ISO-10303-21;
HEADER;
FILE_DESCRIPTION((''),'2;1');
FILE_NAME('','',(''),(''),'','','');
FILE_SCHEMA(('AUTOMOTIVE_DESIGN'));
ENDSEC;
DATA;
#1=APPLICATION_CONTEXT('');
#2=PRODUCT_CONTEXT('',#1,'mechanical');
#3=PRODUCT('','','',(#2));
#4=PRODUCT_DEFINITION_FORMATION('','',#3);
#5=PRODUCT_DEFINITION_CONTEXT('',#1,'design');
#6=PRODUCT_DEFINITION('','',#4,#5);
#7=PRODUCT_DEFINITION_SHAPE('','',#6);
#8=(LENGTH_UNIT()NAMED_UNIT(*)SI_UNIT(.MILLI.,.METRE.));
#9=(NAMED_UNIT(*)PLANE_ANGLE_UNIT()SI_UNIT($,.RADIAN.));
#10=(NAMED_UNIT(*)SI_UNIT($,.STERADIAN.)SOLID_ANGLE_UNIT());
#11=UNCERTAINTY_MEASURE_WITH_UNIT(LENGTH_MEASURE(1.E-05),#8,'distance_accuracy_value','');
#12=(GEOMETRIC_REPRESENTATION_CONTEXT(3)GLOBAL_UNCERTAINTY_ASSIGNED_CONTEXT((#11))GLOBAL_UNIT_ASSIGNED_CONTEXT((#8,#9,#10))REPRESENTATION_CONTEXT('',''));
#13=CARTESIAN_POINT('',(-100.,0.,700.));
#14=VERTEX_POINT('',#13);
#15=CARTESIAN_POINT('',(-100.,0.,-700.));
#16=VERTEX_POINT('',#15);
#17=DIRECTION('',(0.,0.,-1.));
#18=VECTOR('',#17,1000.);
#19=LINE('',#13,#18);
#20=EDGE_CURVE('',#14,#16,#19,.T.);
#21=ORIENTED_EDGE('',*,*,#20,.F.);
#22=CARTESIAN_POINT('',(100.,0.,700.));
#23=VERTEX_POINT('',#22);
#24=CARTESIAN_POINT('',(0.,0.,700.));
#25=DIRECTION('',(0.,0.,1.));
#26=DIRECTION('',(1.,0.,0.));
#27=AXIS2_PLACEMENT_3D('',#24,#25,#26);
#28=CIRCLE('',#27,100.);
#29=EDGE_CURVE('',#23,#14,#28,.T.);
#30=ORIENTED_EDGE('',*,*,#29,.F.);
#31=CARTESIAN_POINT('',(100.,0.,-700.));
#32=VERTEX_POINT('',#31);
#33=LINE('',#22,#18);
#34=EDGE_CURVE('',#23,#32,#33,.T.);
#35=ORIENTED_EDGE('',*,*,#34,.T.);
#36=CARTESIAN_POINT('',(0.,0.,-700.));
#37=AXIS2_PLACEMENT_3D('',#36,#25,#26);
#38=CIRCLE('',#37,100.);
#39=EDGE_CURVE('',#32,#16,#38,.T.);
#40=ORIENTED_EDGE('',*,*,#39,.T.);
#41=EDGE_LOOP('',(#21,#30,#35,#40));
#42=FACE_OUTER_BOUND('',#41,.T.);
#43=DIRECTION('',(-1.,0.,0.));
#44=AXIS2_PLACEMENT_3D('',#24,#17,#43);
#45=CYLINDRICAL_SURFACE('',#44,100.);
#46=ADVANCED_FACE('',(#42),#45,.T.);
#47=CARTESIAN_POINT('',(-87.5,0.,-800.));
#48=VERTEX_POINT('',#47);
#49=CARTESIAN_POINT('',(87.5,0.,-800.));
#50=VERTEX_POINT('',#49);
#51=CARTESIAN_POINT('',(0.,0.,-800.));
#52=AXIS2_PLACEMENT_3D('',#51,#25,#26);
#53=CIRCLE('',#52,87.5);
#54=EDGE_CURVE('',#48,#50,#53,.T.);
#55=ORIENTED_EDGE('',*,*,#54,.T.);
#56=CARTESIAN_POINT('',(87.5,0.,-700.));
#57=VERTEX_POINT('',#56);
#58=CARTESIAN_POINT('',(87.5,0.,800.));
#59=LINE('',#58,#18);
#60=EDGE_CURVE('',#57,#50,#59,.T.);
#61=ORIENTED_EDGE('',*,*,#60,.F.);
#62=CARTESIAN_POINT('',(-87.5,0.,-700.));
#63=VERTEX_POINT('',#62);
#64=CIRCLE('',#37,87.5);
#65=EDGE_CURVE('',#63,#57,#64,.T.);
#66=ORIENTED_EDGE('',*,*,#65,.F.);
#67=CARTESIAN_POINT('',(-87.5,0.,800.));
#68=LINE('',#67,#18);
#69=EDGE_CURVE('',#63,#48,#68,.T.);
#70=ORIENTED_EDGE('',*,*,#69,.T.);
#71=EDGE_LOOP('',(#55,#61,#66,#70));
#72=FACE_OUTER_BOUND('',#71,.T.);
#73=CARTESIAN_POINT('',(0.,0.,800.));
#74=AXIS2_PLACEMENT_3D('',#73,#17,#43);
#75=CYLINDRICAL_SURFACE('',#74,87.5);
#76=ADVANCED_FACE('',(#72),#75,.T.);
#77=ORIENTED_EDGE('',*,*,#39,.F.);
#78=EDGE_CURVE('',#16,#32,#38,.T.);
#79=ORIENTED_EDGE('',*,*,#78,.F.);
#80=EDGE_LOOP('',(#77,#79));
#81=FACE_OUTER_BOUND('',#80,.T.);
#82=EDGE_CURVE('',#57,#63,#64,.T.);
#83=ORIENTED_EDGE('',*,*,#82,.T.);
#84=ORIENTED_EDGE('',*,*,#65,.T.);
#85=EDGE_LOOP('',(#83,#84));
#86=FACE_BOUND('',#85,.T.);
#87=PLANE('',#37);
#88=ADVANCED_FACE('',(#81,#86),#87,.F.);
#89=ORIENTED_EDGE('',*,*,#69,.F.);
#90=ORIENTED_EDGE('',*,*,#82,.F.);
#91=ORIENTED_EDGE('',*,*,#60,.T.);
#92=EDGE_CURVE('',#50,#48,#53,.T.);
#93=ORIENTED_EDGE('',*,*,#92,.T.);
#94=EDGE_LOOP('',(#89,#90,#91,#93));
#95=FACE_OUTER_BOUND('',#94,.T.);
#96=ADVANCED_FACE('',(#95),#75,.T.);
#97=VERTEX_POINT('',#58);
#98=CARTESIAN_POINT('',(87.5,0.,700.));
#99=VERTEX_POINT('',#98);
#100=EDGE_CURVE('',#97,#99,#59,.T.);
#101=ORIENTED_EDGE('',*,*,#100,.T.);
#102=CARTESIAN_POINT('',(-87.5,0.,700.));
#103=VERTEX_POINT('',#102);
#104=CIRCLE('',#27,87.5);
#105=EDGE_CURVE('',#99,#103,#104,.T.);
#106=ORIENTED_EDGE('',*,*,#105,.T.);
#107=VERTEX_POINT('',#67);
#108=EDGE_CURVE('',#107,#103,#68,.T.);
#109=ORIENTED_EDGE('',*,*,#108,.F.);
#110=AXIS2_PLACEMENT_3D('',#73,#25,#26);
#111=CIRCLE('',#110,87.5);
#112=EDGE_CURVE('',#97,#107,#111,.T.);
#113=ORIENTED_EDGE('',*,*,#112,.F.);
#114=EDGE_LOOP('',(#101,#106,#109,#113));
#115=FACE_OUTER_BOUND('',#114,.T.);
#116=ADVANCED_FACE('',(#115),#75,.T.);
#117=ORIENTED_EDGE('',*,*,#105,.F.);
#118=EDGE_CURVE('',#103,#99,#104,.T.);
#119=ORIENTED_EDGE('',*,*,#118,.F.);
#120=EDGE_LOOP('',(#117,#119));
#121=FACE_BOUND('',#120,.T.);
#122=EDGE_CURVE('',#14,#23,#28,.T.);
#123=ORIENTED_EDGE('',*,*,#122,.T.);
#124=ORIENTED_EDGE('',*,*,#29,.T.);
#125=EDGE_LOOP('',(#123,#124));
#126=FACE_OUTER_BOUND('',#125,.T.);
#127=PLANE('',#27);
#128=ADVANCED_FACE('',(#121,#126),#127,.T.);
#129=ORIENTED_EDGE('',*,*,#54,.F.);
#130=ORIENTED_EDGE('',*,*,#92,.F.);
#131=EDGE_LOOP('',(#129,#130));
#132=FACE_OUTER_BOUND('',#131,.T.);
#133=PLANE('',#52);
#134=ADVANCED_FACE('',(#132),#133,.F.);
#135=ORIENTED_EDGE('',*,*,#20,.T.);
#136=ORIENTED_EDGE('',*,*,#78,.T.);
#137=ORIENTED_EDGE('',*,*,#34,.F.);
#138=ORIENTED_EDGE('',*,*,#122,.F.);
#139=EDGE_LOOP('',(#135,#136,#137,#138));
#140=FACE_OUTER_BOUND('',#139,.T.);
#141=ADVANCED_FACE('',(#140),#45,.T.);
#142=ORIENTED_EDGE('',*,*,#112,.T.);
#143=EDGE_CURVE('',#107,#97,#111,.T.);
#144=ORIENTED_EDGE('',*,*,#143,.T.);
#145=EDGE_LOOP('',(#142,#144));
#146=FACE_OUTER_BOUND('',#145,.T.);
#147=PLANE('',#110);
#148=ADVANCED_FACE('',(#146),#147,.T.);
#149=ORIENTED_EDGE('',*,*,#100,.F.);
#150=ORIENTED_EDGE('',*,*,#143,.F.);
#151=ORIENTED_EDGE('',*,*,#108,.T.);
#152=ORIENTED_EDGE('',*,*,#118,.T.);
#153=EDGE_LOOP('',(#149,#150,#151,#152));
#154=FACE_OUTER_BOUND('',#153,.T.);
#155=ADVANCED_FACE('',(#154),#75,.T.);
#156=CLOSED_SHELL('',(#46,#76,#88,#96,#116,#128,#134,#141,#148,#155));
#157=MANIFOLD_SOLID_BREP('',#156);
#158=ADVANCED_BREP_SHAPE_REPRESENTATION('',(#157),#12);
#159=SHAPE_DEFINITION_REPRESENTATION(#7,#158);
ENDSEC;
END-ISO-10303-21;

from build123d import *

# Parameters (mm, degrees)
SKETCH1_R           = 87.5
BOSS_EXTRUDE1_DEPTH = 800
SKETCH2_R           = 100
BOSS_EXTRUDE2_DEPTH = 700


with BuildPart() as part:
    # Sketch1 → Boss-Extrude1 (new, symmetric)
    with BuildSketch(Plane.XY):
        Circle(SKETCH1_R)
    extrude(amount=BOSS_EXTRUDE1_DEPTH, both=True)

    # Sketch2 → Boss-Extrude2 (add, symmetric)
    with BuildSketch(Plane.XY):
        Circle(SKETCH2_R)
    extrude(amount=BOSS_EXTRUDE2_DEPTH, both=True)


solid = part.part
